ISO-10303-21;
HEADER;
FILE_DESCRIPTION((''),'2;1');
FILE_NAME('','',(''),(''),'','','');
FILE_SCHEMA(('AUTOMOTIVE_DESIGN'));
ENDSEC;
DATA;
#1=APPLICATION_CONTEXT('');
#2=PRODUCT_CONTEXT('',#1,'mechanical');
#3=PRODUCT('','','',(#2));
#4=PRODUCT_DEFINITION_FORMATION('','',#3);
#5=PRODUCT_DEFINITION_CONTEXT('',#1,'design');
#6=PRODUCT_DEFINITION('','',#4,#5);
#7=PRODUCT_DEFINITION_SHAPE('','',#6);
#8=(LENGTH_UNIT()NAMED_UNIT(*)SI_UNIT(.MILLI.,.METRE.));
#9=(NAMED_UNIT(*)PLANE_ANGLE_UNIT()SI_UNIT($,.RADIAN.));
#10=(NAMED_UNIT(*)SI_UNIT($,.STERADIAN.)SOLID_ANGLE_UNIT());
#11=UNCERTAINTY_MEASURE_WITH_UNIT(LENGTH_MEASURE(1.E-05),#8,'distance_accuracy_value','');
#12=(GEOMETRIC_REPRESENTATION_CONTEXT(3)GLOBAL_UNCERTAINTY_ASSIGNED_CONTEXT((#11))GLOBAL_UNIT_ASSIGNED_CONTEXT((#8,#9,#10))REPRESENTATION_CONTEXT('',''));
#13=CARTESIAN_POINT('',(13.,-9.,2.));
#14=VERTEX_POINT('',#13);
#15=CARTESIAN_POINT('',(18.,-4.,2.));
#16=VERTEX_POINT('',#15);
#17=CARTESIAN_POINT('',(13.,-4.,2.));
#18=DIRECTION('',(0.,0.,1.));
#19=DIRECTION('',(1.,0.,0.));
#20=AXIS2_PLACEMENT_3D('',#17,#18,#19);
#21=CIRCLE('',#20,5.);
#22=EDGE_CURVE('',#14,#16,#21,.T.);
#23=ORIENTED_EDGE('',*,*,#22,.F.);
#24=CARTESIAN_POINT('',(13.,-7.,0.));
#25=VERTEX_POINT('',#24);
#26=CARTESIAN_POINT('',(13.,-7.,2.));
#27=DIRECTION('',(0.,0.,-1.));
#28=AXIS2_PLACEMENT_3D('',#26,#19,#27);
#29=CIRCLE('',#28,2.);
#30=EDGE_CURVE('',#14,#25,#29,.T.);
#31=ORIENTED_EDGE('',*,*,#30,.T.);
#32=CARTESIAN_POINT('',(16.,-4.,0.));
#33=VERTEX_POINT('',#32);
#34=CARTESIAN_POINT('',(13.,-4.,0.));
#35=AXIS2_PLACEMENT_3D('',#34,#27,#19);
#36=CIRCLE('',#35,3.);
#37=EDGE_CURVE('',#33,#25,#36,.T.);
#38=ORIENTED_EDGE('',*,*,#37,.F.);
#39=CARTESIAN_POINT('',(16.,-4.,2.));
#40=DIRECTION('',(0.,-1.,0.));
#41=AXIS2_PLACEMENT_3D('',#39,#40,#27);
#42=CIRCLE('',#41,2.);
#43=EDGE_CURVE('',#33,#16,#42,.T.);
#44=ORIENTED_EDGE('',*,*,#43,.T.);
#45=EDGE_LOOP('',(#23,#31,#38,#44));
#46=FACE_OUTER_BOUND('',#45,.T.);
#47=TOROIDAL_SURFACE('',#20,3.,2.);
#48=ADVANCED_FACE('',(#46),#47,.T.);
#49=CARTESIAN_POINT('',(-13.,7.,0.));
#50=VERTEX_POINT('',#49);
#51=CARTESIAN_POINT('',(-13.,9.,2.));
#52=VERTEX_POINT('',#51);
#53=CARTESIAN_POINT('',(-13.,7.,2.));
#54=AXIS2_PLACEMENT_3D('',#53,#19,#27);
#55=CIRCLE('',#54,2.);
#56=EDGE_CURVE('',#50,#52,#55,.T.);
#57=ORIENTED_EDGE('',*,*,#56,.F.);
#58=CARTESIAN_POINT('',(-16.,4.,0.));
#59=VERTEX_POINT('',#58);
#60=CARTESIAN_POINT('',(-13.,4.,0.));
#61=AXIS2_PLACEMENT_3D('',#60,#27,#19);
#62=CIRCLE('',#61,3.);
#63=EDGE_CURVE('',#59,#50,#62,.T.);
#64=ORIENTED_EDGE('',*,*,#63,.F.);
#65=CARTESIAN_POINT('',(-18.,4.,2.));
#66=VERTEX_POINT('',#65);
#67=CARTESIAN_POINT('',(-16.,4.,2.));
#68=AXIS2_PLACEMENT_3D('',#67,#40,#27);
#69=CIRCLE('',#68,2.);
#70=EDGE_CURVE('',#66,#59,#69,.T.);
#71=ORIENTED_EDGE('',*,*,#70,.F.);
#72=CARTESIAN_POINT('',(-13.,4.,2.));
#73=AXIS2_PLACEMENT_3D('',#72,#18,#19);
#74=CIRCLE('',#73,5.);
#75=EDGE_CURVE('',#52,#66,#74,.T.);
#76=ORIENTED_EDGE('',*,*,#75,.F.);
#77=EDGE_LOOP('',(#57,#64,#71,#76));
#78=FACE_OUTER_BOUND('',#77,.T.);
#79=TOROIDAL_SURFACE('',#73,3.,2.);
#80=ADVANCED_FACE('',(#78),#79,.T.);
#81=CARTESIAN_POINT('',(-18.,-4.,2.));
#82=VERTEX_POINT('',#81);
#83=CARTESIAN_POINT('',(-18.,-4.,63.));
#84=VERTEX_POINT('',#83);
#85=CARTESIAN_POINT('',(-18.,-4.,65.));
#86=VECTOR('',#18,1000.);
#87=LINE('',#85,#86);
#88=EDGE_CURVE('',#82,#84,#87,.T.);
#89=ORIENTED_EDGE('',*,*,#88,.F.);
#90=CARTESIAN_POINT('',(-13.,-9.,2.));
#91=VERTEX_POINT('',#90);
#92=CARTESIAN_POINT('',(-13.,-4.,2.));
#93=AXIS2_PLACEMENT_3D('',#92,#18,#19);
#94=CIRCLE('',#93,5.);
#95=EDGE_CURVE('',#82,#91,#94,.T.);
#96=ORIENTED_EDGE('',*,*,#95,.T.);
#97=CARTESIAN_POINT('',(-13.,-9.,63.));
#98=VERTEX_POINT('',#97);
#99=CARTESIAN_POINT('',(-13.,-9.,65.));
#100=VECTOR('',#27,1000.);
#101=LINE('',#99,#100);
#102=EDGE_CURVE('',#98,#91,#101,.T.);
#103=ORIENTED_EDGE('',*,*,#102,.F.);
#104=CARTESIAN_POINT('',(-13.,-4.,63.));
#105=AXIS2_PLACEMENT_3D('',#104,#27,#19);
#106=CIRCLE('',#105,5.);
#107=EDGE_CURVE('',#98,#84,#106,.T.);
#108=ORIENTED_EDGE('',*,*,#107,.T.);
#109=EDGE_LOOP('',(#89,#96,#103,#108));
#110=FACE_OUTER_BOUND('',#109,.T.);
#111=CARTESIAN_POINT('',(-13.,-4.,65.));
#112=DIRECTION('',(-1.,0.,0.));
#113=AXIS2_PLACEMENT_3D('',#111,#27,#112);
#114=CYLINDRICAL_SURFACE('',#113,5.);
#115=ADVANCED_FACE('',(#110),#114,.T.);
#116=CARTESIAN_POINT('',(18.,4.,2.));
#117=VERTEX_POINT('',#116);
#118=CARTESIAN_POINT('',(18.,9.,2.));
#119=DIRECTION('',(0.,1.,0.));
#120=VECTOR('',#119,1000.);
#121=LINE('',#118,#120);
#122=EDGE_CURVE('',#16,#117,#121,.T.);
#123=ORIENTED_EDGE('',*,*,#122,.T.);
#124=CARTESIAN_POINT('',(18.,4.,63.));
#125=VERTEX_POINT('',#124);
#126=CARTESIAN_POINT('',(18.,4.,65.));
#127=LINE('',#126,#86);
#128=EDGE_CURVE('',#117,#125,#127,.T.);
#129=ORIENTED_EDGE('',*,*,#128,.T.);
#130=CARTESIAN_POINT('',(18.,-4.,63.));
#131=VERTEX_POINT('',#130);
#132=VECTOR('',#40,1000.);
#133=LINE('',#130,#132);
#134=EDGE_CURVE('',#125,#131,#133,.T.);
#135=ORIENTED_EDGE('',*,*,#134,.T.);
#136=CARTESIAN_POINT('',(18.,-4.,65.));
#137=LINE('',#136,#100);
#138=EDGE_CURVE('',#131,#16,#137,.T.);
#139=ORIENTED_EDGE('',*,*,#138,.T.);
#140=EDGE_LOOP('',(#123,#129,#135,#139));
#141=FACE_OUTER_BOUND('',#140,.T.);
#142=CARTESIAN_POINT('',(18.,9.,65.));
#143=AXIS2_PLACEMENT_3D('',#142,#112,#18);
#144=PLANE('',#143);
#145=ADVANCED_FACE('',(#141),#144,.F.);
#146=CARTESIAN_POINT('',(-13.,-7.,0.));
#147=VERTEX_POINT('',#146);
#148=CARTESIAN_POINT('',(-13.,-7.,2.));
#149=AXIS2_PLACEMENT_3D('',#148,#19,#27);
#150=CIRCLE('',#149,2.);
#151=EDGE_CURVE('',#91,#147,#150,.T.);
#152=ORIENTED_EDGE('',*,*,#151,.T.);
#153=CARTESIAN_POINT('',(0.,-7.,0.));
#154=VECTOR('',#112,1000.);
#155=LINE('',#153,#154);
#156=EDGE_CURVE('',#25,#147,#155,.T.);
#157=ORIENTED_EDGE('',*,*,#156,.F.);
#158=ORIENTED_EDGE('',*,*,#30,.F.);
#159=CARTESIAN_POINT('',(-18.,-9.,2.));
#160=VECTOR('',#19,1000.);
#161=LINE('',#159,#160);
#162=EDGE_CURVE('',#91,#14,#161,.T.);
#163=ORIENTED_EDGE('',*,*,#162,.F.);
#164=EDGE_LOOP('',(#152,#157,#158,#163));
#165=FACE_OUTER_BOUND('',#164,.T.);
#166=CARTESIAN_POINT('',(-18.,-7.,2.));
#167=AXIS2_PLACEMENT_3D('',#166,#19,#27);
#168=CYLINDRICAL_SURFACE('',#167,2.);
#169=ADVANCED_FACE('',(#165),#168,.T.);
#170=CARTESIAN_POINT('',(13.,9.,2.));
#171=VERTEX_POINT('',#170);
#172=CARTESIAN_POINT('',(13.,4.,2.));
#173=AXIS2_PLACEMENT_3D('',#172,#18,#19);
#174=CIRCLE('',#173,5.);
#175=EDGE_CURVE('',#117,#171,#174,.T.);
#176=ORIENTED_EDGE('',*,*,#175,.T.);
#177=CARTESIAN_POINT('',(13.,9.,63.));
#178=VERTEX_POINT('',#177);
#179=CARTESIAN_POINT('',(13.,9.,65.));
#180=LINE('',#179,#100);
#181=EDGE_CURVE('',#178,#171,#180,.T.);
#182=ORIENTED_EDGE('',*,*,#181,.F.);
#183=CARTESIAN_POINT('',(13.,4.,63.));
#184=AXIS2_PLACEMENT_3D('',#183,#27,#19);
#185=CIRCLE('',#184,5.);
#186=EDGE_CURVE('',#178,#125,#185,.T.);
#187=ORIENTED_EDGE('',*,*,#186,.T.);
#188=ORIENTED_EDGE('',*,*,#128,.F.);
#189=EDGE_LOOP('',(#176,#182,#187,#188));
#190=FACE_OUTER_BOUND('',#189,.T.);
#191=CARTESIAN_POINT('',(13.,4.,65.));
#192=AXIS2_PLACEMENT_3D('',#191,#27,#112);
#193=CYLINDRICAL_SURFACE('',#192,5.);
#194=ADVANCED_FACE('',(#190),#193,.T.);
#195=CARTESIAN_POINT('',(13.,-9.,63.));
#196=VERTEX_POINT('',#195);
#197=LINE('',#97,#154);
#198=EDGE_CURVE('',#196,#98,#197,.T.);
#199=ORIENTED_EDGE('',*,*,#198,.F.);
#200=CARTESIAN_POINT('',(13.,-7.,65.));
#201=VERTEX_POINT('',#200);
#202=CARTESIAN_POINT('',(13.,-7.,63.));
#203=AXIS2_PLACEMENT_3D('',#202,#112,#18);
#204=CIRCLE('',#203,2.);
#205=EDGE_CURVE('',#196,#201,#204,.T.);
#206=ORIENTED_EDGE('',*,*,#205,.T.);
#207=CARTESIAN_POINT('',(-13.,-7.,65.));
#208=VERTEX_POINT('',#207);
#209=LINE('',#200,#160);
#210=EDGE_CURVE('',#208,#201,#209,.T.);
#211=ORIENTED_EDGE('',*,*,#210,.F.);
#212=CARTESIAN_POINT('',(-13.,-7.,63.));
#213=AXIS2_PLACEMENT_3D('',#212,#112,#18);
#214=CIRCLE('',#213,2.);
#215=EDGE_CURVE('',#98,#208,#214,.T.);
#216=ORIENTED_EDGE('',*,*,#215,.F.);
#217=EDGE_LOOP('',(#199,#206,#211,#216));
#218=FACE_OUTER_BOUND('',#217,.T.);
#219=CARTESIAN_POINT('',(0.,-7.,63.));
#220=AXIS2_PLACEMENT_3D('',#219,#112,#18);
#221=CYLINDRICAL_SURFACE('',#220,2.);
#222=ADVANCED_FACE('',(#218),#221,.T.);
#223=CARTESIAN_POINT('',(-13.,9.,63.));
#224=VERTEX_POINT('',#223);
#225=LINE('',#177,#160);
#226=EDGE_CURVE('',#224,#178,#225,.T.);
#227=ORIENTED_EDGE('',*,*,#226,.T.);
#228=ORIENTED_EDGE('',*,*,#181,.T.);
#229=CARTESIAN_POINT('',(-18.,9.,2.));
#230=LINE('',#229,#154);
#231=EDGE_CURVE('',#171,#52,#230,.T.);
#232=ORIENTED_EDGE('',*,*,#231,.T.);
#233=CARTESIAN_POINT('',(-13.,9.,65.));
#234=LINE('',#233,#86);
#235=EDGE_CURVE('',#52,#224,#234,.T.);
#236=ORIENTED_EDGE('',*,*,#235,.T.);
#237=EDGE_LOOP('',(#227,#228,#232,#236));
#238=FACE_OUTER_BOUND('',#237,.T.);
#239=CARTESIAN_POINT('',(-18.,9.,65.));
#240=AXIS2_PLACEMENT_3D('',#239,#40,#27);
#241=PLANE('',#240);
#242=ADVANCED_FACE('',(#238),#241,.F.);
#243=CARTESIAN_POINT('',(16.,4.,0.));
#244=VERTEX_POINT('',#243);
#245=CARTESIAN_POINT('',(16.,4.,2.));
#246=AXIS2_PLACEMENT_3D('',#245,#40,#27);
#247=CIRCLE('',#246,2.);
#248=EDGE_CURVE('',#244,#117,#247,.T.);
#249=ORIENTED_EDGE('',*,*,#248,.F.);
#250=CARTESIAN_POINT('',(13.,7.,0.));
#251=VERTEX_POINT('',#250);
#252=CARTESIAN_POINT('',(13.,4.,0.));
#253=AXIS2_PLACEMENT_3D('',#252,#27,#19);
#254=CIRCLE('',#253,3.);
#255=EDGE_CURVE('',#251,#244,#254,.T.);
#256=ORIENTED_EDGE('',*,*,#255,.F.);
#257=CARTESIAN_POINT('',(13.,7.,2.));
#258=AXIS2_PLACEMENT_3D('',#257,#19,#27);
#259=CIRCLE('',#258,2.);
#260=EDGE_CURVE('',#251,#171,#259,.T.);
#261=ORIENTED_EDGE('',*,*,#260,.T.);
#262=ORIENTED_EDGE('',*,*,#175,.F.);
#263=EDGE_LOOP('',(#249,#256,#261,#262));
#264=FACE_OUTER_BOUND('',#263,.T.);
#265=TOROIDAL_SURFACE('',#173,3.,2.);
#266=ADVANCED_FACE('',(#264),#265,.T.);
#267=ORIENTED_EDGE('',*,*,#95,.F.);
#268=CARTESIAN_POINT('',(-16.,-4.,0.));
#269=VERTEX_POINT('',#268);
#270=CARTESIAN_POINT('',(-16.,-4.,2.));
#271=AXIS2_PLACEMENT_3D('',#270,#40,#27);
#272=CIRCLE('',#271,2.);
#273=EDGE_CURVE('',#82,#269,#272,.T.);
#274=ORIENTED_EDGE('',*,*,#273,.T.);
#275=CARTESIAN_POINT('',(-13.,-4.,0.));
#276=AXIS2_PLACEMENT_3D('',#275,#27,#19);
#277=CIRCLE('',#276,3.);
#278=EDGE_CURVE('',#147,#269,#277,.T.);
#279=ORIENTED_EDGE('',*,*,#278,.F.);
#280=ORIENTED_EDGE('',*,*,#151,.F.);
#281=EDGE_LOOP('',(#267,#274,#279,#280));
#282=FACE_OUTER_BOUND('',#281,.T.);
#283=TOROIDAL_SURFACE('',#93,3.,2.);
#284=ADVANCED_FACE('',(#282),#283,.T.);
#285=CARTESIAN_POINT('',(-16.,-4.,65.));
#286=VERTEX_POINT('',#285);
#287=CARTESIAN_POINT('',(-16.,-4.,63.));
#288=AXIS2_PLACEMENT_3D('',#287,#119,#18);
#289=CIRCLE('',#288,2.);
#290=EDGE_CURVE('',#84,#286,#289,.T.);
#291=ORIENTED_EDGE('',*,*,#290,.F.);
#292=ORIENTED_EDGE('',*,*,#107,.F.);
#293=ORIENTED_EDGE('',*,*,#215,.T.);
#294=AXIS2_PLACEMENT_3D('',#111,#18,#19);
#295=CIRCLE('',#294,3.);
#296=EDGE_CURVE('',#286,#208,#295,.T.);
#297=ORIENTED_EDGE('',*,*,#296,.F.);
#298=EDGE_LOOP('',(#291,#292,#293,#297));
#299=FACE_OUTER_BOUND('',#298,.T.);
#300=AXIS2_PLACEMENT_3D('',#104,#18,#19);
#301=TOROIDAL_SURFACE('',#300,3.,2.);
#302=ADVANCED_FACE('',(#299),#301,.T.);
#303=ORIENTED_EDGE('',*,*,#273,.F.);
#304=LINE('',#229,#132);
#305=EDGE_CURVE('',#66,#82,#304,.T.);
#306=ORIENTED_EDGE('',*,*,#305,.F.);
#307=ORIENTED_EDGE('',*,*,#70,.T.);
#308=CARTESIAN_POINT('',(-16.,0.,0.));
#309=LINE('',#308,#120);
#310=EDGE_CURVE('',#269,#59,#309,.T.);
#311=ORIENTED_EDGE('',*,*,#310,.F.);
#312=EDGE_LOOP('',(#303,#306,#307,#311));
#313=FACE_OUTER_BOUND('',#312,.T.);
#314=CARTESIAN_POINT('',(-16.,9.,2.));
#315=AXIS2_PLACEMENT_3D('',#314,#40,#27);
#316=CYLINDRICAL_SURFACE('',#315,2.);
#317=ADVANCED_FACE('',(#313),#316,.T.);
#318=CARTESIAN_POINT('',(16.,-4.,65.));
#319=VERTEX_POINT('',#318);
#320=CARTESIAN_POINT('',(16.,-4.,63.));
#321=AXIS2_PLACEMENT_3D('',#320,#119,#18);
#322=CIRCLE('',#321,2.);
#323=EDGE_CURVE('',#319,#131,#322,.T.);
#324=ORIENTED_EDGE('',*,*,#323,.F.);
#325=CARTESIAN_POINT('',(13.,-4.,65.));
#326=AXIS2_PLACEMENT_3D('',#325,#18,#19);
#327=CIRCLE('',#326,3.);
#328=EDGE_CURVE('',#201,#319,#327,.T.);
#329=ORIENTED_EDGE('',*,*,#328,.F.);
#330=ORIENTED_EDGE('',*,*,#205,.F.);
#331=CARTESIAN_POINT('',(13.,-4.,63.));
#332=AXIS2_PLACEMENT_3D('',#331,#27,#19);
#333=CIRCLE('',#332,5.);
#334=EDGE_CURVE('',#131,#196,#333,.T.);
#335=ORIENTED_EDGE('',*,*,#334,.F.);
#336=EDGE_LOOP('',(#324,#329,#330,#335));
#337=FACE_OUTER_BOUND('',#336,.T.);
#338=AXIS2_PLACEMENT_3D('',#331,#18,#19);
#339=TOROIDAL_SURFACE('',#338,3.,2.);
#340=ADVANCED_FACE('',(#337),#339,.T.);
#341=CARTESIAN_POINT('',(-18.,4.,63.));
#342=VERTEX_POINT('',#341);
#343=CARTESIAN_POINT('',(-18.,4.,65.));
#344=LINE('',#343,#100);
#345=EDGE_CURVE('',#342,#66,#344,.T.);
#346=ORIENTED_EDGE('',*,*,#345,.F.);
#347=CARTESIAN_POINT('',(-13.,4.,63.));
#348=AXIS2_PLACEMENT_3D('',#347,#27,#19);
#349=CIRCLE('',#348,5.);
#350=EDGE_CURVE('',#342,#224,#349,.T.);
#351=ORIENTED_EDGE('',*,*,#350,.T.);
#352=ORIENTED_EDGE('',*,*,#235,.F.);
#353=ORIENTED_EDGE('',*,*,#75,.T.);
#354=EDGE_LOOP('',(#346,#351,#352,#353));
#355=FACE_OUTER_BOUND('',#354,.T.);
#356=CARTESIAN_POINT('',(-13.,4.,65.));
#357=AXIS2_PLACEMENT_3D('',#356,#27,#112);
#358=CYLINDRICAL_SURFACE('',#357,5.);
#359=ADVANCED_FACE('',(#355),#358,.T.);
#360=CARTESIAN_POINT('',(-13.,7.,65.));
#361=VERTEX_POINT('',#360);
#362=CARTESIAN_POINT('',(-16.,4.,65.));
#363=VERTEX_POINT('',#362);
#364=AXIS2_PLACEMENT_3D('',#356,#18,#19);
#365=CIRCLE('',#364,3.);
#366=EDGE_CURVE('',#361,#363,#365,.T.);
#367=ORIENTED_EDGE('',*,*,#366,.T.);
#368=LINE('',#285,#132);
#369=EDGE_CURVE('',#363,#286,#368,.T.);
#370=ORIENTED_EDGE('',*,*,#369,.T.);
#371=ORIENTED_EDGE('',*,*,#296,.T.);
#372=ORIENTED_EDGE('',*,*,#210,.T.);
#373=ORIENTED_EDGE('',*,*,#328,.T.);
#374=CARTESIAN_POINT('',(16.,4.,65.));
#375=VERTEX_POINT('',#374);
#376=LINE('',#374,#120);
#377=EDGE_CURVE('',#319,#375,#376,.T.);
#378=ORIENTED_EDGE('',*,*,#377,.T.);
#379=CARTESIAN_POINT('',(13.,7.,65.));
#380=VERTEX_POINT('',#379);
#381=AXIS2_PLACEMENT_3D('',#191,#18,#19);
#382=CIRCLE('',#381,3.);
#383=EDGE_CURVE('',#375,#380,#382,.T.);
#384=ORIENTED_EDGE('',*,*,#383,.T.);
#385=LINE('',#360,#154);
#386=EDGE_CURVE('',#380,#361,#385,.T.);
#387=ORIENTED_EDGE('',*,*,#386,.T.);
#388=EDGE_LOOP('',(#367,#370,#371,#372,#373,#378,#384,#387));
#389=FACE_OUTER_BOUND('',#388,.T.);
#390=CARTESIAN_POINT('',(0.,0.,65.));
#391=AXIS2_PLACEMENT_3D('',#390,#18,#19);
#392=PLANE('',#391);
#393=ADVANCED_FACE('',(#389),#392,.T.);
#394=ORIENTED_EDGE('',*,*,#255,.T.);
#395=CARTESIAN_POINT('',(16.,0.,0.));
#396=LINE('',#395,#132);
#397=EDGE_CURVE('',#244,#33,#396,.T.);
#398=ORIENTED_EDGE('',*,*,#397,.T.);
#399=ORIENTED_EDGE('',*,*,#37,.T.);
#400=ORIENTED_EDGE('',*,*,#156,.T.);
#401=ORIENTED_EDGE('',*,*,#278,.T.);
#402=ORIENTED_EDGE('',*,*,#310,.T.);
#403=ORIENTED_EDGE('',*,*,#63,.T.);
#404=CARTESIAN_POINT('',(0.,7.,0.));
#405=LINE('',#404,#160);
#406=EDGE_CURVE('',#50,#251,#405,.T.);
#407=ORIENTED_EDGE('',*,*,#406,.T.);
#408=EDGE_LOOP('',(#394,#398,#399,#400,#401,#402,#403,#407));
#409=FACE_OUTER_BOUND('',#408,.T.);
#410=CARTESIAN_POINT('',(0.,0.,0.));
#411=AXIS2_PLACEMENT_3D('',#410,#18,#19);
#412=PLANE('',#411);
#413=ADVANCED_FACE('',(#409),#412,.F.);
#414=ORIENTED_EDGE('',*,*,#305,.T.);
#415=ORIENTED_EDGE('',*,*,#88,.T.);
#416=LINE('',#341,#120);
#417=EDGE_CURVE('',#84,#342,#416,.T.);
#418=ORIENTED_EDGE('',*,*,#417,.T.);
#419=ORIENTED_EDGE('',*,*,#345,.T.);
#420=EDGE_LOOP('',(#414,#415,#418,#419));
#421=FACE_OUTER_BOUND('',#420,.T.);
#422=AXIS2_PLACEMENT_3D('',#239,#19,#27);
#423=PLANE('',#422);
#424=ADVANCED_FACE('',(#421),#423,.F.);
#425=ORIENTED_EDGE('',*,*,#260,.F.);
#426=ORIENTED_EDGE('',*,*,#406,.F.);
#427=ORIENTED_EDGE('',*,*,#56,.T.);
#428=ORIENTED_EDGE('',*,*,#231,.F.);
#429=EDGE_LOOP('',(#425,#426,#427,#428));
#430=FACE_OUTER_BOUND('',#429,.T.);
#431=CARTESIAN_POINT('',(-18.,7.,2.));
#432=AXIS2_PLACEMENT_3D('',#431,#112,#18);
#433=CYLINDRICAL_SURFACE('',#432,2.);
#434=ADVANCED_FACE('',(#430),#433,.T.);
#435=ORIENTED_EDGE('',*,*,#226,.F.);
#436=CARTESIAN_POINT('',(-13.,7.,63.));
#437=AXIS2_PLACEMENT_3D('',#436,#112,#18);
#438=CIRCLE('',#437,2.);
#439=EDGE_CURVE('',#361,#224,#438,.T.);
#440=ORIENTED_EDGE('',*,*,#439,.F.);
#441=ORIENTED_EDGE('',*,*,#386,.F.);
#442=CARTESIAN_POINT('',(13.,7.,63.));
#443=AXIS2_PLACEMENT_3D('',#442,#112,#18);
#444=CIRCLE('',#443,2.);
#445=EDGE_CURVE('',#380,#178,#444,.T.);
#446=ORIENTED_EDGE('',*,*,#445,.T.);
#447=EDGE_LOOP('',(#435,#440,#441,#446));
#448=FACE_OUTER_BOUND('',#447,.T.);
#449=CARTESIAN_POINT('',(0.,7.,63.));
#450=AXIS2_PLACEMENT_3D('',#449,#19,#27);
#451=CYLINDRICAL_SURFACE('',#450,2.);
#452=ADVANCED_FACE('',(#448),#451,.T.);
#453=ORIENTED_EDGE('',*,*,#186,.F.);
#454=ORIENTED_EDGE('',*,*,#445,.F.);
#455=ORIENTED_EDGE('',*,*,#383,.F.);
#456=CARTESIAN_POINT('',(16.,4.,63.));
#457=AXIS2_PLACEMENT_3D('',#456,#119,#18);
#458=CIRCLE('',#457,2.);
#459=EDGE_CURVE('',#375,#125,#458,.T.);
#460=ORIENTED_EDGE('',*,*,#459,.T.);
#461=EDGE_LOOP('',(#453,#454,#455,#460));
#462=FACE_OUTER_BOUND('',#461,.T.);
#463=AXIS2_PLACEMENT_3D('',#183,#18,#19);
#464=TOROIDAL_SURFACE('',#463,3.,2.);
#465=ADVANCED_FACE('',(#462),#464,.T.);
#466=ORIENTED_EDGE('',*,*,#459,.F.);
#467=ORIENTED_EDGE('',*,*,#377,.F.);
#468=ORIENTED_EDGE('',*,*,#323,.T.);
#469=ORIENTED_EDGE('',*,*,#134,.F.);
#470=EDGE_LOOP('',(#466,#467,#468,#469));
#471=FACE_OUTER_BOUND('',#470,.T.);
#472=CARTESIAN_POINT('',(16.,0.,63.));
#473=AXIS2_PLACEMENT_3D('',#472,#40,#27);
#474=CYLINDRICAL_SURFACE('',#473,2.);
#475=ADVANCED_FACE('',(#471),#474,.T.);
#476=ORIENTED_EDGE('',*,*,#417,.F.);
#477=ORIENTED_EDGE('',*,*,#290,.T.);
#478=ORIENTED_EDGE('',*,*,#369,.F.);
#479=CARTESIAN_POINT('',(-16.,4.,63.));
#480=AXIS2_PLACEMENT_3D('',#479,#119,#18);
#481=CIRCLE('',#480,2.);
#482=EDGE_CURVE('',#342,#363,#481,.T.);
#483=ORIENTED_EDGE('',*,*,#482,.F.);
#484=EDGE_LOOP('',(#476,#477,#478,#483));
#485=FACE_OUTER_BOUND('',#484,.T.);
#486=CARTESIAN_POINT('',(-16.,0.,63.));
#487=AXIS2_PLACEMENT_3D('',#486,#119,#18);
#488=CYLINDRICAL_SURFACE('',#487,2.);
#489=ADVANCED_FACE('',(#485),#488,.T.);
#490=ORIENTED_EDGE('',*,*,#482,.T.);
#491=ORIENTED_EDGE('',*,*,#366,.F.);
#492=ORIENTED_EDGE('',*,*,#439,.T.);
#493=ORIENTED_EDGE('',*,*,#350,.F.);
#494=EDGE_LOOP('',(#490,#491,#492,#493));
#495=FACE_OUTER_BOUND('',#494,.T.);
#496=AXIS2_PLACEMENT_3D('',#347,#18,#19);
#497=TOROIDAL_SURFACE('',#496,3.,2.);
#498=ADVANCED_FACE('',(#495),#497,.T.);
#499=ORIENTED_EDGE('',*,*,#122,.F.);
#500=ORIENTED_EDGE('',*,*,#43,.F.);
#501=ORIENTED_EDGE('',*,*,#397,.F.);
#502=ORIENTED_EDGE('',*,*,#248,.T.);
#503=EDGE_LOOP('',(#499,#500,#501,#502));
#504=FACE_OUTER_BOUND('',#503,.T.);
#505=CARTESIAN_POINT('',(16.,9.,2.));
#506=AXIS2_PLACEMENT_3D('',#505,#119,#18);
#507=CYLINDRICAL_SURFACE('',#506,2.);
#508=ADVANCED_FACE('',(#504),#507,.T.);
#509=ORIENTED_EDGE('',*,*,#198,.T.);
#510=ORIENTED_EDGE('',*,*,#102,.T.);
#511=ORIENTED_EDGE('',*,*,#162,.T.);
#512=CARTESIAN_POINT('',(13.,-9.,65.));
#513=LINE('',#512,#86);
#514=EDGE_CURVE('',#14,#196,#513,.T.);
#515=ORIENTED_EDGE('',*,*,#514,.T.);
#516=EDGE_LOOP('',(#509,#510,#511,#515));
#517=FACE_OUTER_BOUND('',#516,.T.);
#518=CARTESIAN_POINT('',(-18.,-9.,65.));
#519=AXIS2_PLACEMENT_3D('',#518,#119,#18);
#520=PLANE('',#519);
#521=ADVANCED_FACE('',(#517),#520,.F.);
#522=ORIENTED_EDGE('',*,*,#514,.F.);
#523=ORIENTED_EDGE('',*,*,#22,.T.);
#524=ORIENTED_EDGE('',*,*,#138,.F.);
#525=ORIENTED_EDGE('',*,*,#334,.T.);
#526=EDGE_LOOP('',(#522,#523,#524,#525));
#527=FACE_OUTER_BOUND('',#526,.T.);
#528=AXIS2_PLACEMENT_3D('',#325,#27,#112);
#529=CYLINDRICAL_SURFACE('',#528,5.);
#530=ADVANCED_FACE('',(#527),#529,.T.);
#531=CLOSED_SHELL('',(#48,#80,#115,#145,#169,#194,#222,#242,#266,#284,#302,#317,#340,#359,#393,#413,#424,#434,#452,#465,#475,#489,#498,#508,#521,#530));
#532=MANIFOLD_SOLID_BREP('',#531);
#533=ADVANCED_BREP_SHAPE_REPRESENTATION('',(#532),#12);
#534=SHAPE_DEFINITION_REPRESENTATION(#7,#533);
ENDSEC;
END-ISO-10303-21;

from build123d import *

# Parameters (mm, degrees)
SKETCH1_W           = 36
SKETCH1_H           = 18
BOSS_EXTRUDE1_DEPTH = 65
FILLET1_R           = 5
FILLET2_R           = 2


with BuildPart() as part:
    # Sketch1 → Boss-Extrude1 (new body)
    with BuildSketch(Plane.XY):
        Rectangle(SKETCH1_W, SKETCH1_H)
    extrude(amount=BOSS_EXTRUDE1_DEPTH)

    # Fillet1
    fillet1_edges = [part.edges().sort_by_distance(p)[0] for p in [
        (18, -9, 32.5),
        (-18, -9, 32.5),
        (-18, 9, 32.5),
        (18, 9, 32.5),
    ]]
    fillet(fillet1_edges, radius=FILLET1_R)

    # Fillet2
    fillet2_edges = [part.edges().sort_by_distance(p)[0] for p in [
        (0, -9, 0),
        (0, -9, 65),
        (18, 0, 0),
        (-18, 0, 0),
        (0, 9, 0),
        (16.535533906, 7.535533906, 0),
        (16.535533906, -7.535533906, 0),
        (-16.535533906, 7.535533906, 0),
        (-16.535533906, -7.535533906, 0),
        (-18, 0, 65),
        (18, 0, 65),
        (0, 9, 65),
        (16.535533906, 7.535533906, 65),
        (16.535533906, -7.535533906, 65),
        (-16.535533906, 7.535533906, 65),
        (-16.535533906, -7.535533906, 65),
    ]]
    fillet(fillet2_edges, radius=FILLET2_R)


solid = part.part
